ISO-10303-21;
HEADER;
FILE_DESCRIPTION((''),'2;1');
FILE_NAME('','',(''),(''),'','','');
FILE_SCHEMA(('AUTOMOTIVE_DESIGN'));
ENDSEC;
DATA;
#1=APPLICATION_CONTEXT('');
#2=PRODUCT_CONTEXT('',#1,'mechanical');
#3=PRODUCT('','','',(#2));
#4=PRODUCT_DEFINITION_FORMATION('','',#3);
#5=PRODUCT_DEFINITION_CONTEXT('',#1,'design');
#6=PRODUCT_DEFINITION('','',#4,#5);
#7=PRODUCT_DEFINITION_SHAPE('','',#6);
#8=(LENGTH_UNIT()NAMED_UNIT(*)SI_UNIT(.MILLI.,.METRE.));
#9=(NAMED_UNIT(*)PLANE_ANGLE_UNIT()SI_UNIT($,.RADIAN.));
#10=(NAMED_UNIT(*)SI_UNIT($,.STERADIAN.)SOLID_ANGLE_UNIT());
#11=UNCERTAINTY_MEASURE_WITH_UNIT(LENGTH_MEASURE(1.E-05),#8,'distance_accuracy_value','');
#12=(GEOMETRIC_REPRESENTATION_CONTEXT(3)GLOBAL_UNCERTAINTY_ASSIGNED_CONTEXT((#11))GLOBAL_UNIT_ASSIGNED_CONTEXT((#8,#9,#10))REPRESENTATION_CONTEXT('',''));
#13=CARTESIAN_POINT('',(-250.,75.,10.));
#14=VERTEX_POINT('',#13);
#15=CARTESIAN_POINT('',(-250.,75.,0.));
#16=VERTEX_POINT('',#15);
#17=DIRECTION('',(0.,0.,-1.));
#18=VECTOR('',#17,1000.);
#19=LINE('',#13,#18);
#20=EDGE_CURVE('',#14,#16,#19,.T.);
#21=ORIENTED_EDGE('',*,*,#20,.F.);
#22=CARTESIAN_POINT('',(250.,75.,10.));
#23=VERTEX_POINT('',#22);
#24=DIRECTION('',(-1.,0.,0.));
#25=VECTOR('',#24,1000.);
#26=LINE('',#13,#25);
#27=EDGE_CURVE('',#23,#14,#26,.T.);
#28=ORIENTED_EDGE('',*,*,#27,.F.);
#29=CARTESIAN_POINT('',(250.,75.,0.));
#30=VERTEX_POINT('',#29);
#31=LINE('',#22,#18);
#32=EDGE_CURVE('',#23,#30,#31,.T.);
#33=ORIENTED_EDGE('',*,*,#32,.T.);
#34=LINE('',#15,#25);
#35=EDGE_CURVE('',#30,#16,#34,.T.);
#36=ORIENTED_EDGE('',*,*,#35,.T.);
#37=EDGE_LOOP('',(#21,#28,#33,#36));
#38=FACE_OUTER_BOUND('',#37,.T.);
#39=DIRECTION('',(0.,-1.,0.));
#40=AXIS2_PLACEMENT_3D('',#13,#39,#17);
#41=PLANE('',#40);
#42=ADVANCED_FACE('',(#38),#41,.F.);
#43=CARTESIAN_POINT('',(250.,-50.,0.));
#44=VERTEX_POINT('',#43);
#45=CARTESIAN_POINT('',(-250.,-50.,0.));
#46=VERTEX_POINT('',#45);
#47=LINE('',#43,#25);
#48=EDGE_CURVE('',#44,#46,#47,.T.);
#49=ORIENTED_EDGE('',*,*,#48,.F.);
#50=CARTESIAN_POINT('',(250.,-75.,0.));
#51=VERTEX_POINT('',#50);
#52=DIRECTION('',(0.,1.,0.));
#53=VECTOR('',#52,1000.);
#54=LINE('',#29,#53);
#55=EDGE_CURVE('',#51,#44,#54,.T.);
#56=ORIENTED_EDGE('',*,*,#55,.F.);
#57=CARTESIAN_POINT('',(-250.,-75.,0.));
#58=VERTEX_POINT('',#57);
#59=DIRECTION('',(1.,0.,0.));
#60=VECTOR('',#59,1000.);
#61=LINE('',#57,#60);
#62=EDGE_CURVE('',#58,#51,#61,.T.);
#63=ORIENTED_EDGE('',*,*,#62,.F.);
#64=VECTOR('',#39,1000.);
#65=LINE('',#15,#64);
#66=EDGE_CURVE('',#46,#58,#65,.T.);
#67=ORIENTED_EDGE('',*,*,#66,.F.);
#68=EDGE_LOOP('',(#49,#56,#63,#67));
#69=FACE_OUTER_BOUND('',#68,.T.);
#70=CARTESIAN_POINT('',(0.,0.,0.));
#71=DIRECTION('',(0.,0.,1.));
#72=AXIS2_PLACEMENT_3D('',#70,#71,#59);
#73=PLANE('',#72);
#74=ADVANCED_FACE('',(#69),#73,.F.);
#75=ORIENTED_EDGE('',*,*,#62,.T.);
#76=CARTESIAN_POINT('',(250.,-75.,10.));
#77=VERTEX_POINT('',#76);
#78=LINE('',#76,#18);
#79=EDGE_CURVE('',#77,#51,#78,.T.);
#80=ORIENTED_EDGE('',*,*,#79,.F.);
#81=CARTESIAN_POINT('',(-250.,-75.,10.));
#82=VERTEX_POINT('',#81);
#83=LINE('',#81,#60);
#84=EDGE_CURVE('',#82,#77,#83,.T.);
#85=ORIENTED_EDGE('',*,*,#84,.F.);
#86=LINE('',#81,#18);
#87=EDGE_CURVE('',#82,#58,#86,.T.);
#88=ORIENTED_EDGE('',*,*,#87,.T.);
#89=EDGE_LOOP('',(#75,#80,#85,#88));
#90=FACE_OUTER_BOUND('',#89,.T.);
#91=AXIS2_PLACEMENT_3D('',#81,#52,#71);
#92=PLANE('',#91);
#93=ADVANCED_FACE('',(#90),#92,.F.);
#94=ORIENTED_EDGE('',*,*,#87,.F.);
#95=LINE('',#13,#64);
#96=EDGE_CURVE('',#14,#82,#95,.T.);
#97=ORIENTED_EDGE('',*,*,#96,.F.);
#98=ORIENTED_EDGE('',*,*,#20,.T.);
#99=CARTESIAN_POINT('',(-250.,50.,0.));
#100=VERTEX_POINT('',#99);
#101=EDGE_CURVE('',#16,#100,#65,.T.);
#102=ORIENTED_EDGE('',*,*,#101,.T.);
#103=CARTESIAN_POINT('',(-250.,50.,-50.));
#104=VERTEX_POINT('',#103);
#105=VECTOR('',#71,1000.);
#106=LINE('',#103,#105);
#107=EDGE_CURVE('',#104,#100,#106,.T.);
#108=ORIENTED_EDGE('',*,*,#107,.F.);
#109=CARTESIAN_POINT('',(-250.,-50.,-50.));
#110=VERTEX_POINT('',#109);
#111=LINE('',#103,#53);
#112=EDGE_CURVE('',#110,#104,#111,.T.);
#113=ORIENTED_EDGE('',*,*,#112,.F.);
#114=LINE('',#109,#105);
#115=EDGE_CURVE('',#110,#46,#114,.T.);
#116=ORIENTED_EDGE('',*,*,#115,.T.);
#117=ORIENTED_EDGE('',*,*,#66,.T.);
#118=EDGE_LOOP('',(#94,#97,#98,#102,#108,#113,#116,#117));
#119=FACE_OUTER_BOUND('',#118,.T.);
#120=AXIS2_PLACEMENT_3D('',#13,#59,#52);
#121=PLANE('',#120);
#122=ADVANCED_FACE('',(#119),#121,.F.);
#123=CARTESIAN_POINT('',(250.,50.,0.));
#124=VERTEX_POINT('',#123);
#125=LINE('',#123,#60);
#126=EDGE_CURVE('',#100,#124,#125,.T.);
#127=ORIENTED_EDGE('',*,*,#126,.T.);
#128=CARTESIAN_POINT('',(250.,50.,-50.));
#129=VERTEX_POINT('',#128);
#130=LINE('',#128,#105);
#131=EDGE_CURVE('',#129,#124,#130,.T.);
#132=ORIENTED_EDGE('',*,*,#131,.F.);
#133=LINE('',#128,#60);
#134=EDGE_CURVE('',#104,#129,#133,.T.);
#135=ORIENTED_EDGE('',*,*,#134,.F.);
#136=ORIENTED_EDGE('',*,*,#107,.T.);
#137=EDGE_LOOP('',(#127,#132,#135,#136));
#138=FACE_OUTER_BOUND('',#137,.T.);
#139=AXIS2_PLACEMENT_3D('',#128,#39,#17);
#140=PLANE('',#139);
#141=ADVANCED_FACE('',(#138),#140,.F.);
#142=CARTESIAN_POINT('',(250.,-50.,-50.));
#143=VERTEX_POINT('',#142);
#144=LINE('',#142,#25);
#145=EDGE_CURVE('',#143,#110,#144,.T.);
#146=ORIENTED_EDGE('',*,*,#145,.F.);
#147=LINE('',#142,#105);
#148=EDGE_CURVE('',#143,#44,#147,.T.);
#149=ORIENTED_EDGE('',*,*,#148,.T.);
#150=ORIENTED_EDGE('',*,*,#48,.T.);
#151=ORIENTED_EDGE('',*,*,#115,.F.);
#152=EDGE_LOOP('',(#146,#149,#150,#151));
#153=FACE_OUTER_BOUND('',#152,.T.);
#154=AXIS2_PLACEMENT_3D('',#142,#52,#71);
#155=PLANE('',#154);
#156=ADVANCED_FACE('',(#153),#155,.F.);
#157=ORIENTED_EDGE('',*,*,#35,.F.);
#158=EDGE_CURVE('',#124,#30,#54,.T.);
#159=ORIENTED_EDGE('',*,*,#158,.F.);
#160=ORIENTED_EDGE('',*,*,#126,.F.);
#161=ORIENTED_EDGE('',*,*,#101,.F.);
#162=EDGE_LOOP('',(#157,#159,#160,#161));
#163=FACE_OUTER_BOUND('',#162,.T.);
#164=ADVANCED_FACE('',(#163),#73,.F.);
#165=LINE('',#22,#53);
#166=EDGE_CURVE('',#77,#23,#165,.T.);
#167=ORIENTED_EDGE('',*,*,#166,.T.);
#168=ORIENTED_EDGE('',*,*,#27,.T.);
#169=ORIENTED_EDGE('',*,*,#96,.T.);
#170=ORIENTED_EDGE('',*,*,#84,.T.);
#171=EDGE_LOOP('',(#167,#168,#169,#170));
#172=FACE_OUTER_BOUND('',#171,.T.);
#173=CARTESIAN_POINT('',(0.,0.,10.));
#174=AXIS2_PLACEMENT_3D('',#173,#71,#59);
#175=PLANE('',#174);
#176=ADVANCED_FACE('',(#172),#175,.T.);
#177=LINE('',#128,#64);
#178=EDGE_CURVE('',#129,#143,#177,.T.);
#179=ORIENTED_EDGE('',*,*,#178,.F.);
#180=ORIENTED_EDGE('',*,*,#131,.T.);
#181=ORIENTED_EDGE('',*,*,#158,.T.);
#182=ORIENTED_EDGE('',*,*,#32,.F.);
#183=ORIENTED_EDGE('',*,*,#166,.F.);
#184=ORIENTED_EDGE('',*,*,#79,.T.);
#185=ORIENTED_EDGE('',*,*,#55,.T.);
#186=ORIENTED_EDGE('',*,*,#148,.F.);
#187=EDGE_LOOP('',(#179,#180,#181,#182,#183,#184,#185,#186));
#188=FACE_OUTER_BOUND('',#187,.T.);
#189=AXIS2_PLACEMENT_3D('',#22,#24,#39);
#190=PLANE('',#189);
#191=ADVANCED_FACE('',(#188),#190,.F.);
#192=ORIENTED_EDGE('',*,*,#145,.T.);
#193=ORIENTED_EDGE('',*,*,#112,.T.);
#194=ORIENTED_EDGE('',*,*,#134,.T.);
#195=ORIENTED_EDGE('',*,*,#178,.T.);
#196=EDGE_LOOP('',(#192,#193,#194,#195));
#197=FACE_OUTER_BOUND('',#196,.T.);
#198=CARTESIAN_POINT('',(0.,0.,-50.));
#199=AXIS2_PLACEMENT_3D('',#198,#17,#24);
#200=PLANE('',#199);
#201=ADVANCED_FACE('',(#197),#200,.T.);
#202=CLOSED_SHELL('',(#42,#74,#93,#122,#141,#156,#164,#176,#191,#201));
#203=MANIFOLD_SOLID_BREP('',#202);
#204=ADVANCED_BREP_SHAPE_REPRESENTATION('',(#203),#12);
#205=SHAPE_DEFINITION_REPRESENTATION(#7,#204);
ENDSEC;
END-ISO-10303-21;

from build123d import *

# Parameters (mm, degrees)
SKETCH1_W           = 500
SKETCH1_H           = 150
BOSS_EXTRUDE1_DEPTH = 10
SKETCH2_W           = 500
SKETCH2_H           = 100
BOSS_EXTRUDE2_DEPTH = 50


with BuildPart() as part:
    # Sketch1 → Boss-Extrude1 (new body)
    with BuildSketch(Plane.XY):
        Rectangle(SKETCH1_W, SKETCH1_H)
    extrude(amount=BOSS_EXTRUDE1_DEPTH)

    # Sketch2 → Boss-Extrude2 (add)
    with BuildSketch(Plane(origin=(0, 0, 0), x_dir=(-1, 0, 0), z_dir=(0, 0, -1))):
        Rectangle(SKETCH2_W, SKETCH2_H)
    extrude(amount=BOSS_EXTRUDE2_DEPTH)


solid = part.part
